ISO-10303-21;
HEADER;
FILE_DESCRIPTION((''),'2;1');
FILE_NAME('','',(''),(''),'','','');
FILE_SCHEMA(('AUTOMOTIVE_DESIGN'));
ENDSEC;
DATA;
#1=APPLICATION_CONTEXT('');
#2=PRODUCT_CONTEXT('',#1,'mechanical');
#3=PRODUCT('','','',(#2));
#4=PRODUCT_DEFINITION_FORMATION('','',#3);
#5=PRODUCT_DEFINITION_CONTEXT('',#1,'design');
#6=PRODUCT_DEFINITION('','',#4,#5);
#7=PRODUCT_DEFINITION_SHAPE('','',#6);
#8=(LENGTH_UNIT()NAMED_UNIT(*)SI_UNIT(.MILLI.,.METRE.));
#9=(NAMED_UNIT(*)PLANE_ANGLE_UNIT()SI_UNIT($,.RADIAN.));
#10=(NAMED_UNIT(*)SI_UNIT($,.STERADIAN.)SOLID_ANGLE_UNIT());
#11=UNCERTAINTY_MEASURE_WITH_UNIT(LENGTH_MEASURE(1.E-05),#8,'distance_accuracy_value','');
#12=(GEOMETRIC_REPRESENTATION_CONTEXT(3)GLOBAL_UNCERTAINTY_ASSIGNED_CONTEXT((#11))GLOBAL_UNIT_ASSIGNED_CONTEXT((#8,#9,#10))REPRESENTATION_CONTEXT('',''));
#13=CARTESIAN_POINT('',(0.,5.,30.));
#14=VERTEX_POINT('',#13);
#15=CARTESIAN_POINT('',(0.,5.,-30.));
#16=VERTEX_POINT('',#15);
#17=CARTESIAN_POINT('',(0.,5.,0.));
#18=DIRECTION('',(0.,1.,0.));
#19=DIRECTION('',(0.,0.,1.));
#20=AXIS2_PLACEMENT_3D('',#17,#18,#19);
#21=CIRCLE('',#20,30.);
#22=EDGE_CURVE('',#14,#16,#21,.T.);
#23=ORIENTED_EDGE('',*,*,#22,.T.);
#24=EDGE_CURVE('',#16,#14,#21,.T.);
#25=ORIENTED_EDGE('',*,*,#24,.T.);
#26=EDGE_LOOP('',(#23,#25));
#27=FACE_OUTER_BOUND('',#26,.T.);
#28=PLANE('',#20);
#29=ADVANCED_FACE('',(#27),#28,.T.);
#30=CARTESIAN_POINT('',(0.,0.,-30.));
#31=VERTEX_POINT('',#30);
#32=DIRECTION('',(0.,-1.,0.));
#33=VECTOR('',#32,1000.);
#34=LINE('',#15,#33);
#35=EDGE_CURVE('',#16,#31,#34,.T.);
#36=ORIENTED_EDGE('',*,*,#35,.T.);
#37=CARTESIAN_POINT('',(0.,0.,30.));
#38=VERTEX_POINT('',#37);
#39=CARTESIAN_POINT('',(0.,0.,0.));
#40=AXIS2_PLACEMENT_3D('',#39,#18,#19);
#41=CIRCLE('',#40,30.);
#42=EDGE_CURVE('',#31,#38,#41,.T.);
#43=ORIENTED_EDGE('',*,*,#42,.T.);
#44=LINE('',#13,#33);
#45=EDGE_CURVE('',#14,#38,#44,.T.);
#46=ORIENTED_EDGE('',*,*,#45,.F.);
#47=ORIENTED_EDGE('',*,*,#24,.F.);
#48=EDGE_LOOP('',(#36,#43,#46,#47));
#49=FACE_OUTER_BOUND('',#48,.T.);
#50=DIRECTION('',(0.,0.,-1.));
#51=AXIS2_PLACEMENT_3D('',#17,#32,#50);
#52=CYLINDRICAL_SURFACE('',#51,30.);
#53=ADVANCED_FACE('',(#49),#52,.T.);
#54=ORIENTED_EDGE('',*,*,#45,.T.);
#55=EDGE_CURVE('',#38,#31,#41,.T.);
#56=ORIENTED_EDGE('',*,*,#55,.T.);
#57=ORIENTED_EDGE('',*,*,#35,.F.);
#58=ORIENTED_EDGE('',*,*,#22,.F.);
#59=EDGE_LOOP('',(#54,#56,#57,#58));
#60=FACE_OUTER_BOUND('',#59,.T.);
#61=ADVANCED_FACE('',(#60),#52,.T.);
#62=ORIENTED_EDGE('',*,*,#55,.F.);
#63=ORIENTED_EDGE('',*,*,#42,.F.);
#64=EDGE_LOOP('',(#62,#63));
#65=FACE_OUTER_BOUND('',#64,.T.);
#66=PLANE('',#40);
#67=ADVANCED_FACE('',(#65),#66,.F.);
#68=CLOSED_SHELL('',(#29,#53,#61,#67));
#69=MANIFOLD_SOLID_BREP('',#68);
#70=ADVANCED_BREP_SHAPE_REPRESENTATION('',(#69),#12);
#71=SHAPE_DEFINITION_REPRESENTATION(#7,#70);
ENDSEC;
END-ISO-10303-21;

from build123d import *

# Parameters (mm, degrees)
SKETCH1_R           = 30
BOSS_EXTRUDE1_DEPTH = 5


with BuildPart() as part:
    # Sketch1 → Boss-Extrude1 (new body)
    with BuildSketch(Plane(origin=(0, 0, 0), x_dir=(1, 0, 0), z_dir=(0, 1, 0))):
        with Locations(Location((0, 0, 0), (0, 0, 270))):
            Circle(SKETCH1_R)
    extrude(amount=BOSS_EXTRUDE1_DEPTH)


solid = part.part
